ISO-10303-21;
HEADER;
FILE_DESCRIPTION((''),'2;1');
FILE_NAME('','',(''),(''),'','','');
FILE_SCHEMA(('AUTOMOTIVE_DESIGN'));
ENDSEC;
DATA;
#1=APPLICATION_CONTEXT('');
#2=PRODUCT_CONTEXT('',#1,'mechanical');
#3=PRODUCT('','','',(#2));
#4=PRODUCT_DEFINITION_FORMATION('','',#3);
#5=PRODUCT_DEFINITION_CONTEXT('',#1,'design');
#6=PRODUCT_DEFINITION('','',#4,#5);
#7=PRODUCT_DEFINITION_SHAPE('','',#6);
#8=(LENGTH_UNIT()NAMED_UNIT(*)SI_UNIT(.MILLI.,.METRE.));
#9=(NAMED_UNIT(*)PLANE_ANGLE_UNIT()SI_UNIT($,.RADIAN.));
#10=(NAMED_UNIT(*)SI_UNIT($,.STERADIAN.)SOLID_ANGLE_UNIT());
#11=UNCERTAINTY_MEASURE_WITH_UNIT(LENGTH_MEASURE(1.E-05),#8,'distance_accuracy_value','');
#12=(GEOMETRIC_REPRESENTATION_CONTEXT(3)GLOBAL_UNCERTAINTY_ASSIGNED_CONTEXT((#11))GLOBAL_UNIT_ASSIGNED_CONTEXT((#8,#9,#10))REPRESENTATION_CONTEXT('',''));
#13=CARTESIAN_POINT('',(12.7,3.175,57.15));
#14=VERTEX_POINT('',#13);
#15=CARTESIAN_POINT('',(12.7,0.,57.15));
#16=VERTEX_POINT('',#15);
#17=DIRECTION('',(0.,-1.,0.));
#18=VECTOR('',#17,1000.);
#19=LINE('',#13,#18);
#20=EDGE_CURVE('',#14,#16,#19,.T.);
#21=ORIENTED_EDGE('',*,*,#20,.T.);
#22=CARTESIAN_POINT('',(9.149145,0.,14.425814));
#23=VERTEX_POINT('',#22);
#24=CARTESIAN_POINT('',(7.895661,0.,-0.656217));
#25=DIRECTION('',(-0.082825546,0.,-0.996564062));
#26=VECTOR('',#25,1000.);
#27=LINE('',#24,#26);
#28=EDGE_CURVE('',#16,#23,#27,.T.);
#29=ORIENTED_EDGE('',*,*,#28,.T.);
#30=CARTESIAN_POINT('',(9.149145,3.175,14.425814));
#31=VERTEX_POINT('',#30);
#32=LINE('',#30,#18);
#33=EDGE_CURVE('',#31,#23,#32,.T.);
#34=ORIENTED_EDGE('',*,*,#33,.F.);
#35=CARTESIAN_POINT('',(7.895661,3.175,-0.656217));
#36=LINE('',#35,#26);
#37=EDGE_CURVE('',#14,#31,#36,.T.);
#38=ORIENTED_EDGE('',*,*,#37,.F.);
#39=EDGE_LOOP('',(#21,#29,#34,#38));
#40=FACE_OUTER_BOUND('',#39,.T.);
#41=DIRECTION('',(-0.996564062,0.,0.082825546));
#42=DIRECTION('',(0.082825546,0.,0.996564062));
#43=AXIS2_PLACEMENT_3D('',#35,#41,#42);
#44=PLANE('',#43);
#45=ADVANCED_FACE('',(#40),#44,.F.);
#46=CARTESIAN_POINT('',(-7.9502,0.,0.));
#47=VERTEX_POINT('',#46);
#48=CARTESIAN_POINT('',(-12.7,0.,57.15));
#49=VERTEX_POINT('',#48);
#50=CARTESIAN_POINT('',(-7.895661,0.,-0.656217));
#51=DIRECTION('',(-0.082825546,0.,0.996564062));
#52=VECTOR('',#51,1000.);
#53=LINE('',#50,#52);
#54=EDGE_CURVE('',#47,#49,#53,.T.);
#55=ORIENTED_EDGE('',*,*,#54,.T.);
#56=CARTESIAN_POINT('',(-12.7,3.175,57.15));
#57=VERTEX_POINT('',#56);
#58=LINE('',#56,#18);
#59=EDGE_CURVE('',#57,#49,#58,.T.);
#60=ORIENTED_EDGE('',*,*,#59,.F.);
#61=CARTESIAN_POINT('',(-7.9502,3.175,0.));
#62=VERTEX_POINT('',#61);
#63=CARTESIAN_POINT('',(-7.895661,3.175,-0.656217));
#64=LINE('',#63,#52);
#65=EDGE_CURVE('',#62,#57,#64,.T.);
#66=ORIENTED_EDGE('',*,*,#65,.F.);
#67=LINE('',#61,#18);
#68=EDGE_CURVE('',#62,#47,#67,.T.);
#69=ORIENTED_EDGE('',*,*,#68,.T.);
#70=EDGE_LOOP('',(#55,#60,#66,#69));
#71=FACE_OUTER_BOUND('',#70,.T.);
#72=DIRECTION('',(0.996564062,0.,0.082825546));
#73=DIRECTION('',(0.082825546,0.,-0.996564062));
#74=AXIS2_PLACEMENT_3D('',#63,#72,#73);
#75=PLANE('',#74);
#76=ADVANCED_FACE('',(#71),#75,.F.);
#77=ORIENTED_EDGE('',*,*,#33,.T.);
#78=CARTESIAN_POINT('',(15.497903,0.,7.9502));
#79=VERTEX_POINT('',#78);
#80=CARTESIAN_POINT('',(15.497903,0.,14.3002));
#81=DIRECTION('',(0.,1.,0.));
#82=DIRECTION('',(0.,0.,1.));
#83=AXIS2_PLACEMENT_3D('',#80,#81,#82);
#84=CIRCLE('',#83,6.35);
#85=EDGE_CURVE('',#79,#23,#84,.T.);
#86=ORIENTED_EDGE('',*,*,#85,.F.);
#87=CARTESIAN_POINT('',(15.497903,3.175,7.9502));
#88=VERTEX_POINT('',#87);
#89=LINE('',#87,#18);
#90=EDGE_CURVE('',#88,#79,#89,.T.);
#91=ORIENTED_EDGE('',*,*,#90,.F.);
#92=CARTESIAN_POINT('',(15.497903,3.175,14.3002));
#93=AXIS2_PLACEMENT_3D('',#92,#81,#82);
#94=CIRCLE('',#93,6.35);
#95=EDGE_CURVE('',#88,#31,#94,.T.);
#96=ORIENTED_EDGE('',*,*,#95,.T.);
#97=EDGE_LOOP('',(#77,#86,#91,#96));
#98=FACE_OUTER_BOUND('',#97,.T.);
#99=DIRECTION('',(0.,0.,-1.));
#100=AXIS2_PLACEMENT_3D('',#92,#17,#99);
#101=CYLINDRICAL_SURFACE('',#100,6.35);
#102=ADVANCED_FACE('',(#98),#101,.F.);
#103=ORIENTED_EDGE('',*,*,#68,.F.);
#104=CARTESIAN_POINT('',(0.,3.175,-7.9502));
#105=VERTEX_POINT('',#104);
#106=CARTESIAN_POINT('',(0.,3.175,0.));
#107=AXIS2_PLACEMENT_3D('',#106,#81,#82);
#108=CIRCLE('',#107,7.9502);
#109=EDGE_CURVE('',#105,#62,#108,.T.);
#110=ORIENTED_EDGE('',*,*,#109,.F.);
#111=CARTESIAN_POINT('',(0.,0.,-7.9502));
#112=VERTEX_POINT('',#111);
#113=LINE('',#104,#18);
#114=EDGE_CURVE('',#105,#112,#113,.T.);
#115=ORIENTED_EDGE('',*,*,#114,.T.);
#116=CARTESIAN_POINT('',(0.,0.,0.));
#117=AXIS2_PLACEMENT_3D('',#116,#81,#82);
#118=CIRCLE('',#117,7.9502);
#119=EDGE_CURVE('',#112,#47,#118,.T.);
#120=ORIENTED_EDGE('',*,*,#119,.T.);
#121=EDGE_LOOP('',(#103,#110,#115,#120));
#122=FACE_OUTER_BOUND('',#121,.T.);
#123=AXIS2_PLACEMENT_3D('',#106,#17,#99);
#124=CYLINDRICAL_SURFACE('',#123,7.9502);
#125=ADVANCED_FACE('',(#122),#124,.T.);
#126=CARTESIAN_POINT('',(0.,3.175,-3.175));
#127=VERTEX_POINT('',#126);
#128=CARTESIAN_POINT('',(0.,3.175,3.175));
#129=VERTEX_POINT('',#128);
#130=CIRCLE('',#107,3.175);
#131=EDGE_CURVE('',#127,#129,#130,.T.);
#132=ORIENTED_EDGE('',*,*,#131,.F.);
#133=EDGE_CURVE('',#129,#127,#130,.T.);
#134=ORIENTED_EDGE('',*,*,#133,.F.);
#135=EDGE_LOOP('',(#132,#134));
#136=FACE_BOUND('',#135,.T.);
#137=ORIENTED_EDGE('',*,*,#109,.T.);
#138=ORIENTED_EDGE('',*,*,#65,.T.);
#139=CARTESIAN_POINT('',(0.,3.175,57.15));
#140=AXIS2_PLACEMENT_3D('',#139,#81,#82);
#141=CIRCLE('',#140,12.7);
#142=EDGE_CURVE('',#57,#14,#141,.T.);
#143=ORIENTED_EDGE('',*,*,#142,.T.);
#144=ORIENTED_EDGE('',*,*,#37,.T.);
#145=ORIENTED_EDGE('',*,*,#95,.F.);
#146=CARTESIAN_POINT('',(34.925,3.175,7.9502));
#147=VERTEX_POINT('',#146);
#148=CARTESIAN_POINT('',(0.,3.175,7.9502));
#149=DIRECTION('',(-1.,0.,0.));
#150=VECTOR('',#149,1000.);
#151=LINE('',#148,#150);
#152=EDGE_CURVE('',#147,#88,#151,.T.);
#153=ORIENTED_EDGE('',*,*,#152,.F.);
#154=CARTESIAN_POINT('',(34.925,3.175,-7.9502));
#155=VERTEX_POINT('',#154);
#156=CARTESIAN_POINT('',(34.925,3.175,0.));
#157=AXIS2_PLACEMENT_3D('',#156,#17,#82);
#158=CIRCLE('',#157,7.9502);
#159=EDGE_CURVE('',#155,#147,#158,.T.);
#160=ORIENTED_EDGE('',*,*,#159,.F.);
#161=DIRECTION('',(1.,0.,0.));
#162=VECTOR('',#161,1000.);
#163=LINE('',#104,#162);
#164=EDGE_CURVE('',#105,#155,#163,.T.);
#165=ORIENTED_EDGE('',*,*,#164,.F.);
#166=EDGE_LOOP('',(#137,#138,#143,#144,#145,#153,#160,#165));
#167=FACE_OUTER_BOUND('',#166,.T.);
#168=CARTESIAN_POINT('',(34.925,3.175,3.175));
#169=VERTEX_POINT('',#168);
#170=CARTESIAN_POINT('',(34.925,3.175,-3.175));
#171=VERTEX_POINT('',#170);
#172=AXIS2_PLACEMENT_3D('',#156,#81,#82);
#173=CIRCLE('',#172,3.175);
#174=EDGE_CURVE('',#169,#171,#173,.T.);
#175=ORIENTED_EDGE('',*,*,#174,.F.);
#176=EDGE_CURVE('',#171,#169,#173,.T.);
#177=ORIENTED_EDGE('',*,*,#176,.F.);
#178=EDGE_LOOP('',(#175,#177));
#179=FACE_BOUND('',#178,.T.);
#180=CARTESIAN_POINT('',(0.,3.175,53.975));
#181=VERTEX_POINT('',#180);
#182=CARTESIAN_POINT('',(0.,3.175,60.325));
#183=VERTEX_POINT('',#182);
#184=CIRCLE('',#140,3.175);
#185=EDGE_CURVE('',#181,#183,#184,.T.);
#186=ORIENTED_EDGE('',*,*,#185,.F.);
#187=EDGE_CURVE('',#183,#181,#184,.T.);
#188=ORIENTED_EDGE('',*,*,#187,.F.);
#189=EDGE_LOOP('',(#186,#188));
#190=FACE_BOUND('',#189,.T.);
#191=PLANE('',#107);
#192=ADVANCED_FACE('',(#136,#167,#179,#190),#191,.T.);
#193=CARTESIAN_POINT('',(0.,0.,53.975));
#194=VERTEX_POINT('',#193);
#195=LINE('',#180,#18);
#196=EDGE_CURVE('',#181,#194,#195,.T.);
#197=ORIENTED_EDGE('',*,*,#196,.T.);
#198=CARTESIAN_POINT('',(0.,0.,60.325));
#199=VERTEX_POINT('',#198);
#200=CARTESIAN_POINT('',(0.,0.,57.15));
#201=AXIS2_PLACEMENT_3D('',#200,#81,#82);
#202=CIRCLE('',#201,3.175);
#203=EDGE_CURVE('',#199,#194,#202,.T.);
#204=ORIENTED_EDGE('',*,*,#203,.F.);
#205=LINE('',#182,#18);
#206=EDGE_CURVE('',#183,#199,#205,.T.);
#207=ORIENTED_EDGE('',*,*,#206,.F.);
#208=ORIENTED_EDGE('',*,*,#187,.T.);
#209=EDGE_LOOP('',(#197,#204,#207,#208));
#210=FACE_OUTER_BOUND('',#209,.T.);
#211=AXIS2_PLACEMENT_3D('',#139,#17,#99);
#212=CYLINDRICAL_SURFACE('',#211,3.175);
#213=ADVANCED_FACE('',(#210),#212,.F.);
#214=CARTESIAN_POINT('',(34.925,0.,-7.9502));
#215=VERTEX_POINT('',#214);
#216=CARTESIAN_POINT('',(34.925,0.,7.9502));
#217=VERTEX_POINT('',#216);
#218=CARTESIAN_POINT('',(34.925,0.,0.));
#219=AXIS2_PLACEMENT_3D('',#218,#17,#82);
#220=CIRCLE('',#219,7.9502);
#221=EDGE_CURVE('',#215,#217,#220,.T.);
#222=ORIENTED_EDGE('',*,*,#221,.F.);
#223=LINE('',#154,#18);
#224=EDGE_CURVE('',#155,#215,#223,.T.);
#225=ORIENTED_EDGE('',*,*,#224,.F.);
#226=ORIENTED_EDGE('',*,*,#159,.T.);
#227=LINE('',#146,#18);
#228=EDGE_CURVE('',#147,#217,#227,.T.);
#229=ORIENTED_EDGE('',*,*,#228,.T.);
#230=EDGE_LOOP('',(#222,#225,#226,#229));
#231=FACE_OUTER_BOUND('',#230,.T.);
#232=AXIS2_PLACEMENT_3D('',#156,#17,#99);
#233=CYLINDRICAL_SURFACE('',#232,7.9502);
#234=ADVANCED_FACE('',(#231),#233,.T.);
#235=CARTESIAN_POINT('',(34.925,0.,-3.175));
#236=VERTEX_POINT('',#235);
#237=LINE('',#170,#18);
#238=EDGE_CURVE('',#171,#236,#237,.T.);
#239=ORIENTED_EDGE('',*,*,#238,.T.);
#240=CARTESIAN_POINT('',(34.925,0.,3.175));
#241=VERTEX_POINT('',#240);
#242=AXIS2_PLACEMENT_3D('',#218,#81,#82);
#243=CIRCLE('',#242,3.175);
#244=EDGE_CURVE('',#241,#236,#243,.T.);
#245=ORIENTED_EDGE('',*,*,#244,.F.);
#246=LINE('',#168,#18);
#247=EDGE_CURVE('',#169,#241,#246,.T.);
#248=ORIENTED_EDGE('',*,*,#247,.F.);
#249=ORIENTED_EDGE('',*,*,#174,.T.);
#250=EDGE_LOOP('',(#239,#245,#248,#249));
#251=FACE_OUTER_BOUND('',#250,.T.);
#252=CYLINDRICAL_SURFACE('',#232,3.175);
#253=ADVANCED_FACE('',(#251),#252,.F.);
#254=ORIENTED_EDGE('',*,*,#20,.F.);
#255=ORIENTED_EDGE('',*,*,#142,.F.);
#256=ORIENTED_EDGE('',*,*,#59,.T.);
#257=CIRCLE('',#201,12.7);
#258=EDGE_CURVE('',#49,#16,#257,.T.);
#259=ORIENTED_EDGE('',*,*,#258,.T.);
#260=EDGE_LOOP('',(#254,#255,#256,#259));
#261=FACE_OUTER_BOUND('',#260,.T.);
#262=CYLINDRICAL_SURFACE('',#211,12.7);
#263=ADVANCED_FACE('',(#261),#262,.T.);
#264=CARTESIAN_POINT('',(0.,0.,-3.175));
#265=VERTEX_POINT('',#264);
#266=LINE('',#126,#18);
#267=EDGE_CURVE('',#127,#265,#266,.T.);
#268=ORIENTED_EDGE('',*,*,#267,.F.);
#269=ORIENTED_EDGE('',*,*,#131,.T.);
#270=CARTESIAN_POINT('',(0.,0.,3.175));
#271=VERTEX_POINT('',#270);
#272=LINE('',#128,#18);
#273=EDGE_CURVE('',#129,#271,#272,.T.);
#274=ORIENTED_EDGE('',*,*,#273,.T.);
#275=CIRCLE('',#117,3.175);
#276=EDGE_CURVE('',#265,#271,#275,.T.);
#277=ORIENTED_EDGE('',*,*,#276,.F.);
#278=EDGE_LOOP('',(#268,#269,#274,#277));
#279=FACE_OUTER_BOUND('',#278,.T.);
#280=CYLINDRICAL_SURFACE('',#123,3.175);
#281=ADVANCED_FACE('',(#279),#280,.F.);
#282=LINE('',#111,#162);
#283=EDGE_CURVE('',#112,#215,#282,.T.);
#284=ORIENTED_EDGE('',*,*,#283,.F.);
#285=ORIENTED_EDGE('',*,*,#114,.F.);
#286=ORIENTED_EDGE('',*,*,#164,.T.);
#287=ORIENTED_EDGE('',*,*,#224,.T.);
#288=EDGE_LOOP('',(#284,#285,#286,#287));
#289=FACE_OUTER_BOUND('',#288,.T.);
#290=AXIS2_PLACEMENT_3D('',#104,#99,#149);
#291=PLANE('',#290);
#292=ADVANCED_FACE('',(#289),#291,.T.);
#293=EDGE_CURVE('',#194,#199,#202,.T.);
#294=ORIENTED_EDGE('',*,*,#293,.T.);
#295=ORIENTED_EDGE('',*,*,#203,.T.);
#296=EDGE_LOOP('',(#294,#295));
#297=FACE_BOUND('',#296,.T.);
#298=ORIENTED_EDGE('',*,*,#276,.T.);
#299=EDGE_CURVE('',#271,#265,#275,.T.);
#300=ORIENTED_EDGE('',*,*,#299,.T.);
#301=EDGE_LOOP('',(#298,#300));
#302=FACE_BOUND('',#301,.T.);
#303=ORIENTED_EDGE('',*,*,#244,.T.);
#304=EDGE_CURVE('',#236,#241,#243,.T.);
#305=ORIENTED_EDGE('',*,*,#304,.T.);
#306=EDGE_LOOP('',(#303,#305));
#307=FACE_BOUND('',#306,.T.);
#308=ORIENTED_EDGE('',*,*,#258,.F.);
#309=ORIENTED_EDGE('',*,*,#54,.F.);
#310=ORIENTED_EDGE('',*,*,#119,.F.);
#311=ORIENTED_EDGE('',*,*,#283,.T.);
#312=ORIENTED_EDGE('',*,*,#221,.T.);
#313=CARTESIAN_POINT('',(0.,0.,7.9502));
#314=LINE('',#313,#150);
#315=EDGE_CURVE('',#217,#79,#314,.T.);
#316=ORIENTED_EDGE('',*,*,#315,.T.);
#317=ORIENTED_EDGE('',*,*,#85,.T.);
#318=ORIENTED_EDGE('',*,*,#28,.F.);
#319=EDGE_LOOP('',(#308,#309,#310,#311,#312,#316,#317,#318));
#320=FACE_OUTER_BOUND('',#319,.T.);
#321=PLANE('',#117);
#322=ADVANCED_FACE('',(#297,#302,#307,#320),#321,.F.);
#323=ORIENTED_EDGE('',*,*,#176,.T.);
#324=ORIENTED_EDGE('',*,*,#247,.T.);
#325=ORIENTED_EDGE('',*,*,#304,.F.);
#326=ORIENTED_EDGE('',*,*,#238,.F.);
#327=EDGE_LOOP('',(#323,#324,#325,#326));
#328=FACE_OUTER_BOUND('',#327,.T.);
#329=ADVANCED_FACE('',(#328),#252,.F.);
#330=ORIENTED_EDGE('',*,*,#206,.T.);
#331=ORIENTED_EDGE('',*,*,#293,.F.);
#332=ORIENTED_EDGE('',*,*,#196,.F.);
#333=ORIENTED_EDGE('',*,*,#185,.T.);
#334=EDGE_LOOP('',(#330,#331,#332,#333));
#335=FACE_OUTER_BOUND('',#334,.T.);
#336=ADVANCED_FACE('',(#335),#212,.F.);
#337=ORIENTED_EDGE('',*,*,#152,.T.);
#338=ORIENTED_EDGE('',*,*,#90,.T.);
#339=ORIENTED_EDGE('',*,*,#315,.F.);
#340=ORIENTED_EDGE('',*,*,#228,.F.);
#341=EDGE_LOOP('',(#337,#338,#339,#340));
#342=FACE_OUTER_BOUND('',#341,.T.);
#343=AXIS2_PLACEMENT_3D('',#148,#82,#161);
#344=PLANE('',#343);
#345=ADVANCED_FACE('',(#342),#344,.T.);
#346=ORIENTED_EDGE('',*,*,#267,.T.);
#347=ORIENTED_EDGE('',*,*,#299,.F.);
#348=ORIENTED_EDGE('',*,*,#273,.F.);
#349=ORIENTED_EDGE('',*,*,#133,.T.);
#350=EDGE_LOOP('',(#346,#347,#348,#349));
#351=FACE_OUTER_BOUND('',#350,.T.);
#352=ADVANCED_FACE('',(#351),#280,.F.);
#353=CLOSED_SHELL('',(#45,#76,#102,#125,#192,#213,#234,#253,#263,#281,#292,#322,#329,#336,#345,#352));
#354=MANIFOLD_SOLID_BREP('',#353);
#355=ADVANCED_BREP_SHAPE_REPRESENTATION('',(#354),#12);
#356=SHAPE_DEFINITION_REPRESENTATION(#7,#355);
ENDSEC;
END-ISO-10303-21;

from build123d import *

# Parameters (mm, degrees)
SKETCH1_R           = 3.175
BOSS_EXTRUDE1_DEPTH = 3.175


with BuildPart() as part:
    # Sketch1 → Boss-Extrude1 (new body)
    with BuildSketch(Plane(origin=(0, 0, 0), x_dir=(1, 0, 0), z_dir=(0, 1, 0))):
        with BuildLine():
            Line((0, 7.9502), (34.925, 7.9502))
            ThreePointArc((34.925, 7.9502), (42.8752, 0), (34.925, -7.9502))
            Line((34.925, -7.9502), (15.497902875, -7.9502))
            ThreePointArc((15.497902875, -7.9502), (10.963581061, -9.854705012), (9.149145427, -14.425813956))
            Line((9.149145427, -14.425813956), (12.7, -57.15))
            ThreePointArc((12.7, -57.15), (0, -69.85), (-12.7, -57.15))
            Line((-12.7, -57.15), (-7.9502, 0))
            ThreePointArc((-7.9502, 0), (-5.621640332, 5.621640332), (0, 7.9502))
        make_face()
        with Locations(Location((34.925, 0, 0), (0, 0, 270))):
            Circle(SKETCH1_R, mode=Mode.SUBTRACT)
        with Locations(Location((0, 0, 0), (0, 0, 270))):
            Circle(SKETCH1_R, mode=Mode.SUBTRACT)
        with Locations(Location((0, -57.15, 0), (0, 0, 270))):
            Circle(SKETCH1_R, mode=Mode.SUBTRACT)
    extrude(amount=BOSS_EXTRUDE1_DEPTH)


solid = part.part
